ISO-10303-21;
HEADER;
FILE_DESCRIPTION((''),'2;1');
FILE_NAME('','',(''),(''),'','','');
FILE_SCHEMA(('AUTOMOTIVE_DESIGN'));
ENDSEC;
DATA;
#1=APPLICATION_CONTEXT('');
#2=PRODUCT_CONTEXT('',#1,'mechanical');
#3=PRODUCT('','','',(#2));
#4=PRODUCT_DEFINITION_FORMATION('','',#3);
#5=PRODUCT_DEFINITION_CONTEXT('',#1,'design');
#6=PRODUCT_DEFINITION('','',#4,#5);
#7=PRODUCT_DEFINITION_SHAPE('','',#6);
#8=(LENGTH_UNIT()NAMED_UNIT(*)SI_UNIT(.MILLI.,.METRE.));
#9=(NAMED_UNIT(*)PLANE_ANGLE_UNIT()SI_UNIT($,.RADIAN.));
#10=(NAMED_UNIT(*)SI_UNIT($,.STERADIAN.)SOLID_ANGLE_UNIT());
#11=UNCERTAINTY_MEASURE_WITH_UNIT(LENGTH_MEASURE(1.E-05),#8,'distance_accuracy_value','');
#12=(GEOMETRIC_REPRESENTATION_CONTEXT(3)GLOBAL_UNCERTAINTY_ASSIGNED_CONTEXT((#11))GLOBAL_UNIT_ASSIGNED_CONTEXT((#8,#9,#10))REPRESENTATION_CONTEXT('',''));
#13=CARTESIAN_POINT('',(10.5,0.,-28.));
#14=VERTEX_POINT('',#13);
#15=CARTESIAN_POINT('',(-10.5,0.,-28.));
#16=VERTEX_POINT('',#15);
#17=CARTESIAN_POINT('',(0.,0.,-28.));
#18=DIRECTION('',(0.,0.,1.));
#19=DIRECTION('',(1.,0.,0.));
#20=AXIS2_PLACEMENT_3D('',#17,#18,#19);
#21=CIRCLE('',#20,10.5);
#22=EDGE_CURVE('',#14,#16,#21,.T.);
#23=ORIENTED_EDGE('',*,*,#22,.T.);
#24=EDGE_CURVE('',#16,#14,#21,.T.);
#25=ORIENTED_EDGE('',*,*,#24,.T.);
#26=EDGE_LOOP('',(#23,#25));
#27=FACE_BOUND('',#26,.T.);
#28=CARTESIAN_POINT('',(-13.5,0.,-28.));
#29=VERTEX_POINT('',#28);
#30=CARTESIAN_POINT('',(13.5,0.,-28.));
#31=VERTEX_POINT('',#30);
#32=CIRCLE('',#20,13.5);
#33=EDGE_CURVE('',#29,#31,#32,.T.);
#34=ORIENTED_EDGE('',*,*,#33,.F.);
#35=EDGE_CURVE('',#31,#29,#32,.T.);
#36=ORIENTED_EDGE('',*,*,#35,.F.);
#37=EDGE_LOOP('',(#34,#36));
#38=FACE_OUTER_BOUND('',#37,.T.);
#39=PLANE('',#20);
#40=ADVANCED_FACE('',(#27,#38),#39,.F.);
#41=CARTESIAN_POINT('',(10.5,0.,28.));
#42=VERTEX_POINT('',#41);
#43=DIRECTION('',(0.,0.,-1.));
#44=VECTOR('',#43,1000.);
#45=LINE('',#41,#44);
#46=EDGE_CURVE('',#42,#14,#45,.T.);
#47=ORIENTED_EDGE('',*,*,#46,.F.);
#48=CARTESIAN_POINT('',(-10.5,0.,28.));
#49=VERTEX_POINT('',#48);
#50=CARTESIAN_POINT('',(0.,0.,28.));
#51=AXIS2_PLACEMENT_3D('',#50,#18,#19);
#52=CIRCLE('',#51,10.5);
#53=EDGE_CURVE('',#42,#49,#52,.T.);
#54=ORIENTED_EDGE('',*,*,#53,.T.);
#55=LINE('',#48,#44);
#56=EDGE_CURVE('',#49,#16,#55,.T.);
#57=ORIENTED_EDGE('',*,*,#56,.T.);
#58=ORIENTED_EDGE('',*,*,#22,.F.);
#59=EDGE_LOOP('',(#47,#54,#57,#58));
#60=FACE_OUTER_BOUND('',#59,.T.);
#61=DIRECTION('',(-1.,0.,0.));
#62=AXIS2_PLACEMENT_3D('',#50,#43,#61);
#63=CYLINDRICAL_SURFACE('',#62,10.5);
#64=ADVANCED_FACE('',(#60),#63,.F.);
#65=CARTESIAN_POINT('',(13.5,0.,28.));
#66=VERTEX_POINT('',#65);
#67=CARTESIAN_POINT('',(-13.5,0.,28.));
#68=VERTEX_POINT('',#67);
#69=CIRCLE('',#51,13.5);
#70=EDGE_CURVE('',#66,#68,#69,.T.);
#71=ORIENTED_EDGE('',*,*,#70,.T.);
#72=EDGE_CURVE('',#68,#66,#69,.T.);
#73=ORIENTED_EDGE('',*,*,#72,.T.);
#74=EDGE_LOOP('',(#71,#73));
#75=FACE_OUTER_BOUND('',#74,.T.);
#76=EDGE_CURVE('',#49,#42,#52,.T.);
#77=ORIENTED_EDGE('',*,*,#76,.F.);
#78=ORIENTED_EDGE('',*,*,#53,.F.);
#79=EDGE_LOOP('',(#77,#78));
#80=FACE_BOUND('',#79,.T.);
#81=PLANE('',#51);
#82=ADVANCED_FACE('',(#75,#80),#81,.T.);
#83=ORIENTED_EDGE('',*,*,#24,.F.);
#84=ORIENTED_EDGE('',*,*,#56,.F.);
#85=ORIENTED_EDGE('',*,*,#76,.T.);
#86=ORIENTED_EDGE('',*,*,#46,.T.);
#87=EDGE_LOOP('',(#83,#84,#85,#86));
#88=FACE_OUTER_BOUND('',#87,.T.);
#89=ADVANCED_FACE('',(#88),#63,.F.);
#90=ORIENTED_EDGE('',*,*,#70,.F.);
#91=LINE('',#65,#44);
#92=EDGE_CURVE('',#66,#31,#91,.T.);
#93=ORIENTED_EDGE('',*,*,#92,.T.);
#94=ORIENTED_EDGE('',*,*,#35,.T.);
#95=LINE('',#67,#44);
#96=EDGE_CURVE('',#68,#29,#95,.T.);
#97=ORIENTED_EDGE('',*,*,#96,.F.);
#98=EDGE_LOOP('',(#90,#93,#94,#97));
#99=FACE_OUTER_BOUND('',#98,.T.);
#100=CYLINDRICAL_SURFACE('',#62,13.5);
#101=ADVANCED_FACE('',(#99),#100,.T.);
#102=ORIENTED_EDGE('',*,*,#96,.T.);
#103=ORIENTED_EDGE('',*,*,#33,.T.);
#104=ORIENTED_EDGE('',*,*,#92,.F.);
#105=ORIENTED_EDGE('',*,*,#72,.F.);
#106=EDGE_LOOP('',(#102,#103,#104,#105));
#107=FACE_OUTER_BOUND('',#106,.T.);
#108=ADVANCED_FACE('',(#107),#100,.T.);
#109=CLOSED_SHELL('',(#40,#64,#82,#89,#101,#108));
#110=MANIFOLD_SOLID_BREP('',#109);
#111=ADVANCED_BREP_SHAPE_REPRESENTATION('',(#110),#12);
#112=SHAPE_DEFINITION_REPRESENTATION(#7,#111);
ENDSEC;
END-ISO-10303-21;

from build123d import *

# Parameters (mm, degrees)
SKETCH1_R           = 13.5
SKETCH1_R_2         = 10.5
BOSS_EXTRUDE1_DEPTH = 28


with BuildPart() as part:
    # Sketch1 → Boss-Extrude1 (new, symmetric)
    with BuildSketch(Plane.XY):
        Circle(SKETCH1_R)
        Circle(SKETCH1_R_2, mode=Mode.SUBTRACT)
    extrude(amount=BOSS_EXTRUDE1_DEPTH, both=True)


solid = part.part
